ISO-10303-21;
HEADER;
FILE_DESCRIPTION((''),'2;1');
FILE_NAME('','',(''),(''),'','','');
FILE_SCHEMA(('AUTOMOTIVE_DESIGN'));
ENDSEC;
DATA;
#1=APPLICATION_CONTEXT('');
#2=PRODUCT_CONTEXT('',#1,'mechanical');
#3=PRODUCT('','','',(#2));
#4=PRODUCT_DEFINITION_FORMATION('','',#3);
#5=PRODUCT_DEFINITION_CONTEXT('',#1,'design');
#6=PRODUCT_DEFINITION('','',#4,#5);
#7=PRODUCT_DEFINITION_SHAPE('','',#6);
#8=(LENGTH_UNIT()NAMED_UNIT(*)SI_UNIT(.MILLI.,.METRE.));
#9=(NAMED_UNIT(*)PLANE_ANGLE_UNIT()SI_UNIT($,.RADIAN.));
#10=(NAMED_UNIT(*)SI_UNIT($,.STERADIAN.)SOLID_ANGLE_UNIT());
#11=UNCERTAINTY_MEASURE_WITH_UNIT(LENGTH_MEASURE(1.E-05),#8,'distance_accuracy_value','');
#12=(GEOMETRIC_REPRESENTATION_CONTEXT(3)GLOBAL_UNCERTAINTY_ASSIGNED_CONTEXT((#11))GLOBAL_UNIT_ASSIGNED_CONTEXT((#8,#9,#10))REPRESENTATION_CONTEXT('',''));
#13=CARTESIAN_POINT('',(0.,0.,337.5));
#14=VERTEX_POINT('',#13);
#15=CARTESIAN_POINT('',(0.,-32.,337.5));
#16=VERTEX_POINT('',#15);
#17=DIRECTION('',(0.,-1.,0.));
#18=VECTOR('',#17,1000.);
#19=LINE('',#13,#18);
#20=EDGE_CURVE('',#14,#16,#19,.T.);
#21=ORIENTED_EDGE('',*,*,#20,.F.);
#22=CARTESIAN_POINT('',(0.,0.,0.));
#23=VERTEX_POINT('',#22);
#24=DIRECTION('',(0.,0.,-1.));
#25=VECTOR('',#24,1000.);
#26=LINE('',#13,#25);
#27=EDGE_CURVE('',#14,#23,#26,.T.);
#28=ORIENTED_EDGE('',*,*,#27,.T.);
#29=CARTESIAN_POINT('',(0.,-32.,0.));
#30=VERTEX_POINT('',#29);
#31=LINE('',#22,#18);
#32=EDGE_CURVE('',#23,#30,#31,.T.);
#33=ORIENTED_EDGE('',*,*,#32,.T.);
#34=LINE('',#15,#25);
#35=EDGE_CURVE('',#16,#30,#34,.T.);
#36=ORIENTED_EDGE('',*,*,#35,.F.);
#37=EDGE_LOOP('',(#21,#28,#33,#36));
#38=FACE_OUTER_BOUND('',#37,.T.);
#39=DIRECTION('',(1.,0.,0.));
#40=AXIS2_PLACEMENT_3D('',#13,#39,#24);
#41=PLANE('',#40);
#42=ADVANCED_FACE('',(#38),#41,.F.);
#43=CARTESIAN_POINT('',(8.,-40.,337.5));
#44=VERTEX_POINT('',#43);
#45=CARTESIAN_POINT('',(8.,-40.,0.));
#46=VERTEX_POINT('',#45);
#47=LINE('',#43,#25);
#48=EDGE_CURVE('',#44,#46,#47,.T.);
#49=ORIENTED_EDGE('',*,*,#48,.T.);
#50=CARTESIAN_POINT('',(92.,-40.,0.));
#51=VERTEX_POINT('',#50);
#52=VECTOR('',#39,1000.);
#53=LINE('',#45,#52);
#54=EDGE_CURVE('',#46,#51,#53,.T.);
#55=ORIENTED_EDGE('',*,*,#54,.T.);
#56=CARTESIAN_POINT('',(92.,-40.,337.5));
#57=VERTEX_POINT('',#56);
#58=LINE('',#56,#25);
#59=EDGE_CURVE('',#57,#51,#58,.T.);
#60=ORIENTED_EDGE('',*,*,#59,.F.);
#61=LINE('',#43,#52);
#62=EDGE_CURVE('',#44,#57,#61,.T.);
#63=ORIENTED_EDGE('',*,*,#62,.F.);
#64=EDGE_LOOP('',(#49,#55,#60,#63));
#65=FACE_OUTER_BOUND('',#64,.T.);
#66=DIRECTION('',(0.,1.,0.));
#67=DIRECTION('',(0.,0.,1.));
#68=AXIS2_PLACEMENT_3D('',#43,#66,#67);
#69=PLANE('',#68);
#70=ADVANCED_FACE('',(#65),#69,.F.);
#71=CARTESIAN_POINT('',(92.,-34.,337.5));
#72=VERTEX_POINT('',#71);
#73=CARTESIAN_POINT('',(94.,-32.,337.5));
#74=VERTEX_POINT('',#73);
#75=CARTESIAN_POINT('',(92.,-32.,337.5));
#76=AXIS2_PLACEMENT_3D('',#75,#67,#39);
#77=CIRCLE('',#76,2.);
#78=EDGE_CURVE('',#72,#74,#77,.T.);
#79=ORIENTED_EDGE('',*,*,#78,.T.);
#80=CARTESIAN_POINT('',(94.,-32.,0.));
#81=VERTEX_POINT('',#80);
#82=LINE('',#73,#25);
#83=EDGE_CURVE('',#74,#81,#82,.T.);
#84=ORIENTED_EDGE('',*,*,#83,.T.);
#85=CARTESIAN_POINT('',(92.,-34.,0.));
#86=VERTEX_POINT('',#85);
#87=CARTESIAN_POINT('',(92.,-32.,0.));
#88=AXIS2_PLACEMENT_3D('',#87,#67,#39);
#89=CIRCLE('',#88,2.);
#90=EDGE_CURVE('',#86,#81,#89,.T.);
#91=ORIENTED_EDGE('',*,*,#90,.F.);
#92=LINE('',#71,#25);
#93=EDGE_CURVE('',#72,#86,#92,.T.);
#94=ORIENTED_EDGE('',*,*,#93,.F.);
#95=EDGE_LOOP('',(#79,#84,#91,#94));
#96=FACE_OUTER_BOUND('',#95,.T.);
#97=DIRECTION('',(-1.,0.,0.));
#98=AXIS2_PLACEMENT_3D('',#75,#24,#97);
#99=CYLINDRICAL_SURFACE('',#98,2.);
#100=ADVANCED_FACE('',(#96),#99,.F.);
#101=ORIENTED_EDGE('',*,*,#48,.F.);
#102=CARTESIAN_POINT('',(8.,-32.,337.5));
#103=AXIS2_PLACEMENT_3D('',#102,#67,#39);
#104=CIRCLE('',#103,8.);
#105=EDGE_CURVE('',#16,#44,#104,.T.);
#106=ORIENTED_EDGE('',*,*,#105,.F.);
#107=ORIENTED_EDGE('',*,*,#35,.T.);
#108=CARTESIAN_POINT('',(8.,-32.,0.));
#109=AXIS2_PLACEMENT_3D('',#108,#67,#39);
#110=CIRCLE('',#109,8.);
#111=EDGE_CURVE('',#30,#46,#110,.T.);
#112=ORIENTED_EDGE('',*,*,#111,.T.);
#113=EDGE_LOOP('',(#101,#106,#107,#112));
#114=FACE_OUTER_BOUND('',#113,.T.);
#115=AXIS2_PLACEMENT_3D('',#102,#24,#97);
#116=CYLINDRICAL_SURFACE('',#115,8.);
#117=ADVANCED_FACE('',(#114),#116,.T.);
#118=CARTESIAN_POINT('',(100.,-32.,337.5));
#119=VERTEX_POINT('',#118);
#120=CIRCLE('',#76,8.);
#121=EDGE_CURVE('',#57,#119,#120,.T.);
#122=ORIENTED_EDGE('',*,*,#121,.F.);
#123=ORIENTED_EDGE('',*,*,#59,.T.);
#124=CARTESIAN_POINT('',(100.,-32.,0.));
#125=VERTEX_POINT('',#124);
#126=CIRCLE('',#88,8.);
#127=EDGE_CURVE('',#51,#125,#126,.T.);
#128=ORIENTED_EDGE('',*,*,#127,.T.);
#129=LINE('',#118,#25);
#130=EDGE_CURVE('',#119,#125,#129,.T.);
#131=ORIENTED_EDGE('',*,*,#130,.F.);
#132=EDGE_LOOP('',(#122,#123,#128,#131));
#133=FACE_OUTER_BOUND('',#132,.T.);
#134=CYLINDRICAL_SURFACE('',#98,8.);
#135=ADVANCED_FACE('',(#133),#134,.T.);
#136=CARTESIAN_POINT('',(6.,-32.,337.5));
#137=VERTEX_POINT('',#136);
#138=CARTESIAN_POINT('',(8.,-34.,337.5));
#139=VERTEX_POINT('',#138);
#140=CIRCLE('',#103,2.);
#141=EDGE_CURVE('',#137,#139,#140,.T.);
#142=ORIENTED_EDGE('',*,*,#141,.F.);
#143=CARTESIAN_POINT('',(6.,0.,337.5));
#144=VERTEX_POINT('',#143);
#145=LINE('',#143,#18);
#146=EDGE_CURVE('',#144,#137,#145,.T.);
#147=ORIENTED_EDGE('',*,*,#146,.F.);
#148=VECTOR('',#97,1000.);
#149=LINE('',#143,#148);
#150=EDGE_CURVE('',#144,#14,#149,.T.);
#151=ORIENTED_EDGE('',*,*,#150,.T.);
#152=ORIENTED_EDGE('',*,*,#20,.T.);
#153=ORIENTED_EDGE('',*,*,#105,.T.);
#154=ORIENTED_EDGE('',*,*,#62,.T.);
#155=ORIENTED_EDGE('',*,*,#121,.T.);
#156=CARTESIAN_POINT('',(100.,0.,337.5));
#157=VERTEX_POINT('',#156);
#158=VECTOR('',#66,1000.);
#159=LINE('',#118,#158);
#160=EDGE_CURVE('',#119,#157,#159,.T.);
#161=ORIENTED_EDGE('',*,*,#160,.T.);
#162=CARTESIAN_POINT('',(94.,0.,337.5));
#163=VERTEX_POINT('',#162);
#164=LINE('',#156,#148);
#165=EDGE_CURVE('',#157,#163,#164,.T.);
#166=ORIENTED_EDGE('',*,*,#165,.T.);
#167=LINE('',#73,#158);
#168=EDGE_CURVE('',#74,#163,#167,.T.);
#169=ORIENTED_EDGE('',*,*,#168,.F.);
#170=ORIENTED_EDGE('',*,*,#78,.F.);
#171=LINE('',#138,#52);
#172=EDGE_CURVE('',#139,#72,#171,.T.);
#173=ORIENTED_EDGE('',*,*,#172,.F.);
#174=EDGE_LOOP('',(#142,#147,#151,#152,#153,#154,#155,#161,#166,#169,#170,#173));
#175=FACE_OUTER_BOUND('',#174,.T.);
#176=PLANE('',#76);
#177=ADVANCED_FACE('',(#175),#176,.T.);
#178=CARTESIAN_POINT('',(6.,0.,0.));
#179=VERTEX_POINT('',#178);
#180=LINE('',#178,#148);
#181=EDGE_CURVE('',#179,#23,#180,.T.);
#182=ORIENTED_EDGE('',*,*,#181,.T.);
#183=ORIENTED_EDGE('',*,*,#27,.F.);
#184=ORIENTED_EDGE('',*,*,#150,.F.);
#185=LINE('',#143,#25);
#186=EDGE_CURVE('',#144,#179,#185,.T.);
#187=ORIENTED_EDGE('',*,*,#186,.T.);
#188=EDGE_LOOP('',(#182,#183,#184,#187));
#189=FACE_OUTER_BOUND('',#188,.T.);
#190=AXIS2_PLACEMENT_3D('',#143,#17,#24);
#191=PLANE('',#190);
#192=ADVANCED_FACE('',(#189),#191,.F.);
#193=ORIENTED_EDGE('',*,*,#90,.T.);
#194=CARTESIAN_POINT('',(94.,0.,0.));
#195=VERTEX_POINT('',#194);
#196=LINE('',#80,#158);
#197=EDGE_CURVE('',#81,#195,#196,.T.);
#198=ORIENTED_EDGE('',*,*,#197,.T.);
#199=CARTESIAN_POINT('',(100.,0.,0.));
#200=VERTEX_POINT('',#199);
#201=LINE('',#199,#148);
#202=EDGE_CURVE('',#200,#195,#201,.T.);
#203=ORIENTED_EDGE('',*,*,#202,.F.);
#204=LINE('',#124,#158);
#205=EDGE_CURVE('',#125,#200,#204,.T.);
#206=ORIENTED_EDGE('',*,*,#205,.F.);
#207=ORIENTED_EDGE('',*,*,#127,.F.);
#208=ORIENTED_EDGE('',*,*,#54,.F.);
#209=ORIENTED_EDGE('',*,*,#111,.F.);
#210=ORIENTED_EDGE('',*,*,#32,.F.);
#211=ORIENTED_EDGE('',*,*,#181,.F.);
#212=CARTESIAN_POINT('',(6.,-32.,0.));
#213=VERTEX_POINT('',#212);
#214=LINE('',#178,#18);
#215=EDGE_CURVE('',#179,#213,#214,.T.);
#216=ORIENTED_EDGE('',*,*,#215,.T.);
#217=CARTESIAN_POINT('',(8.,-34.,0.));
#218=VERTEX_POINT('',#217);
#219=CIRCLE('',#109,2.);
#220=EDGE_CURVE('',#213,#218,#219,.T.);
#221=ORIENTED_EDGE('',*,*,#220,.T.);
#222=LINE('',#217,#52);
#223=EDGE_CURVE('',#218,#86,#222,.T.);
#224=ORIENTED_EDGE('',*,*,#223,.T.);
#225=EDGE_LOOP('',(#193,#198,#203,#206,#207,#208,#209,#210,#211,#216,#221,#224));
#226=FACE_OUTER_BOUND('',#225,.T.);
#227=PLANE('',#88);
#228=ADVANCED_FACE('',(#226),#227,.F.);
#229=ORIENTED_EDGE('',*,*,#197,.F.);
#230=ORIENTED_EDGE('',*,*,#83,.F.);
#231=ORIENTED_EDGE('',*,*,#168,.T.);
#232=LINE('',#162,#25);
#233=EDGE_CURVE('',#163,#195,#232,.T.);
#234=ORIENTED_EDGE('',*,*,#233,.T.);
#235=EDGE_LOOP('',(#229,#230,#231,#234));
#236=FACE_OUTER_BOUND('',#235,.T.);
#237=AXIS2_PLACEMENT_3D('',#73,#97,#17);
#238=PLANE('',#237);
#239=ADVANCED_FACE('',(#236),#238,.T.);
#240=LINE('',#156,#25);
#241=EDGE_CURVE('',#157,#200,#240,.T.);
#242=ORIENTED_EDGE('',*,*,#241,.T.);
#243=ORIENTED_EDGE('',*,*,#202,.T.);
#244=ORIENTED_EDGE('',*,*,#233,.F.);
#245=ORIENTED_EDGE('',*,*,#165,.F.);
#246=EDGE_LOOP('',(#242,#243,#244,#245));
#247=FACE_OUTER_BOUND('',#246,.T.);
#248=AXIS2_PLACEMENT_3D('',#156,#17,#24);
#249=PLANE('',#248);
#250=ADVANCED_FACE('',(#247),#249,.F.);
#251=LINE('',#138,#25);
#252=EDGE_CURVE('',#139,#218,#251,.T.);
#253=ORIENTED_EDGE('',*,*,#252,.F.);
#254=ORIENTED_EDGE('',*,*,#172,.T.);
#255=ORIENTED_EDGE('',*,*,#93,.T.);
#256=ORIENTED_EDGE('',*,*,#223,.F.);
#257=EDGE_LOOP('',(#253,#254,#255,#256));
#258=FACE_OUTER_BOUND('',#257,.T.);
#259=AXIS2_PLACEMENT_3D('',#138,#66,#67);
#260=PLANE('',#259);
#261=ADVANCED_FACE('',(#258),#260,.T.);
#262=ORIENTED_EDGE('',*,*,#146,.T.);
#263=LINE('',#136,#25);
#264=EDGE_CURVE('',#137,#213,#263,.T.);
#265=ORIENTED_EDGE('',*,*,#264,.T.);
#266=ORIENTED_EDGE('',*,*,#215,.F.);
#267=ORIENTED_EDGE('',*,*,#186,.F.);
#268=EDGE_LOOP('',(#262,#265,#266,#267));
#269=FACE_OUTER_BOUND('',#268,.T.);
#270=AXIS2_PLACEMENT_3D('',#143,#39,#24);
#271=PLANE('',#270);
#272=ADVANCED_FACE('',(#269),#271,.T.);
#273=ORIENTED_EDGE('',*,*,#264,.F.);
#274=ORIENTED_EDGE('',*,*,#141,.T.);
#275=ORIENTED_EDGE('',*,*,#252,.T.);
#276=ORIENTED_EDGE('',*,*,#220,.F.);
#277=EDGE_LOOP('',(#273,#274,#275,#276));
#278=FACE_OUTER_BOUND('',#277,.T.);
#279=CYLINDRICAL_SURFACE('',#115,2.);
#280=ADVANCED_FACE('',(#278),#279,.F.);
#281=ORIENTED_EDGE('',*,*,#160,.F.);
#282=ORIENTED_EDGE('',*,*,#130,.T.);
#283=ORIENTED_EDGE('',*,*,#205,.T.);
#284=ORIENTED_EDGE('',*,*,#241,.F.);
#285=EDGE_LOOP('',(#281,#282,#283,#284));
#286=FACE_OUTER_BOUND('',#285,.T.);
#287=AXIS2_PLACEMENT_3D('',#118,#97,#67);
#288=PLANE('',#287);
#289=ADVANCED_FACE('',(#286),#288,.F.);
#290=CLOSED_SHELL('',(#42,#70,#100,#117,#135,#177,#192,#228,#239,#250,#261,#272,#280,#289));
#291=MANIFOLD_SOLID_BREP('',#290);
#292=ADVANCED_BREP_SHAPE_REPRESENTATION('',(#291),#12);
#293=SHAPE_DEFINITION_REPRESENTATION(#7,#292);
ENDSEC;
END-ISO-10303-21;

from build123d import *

# Parameters (mm, degrees)
BOSS_EXTRUDE2_DEPTH = 337.5


with BuildPart() as part:
    # Sketch2 → Boss-Extrude2 (new body)
    with BuildSketch(Plane.XY):
        with BuildLine():
            Line((0, 0), (0, -32))
            ThreePointArc((0, -32), (2.343145751, -37.656854249), (8, -40))
            Line((8, -40), (92, -40))
            ThreePointArc((92, -40), (97.656854249, -37.656854249), (100, -32))
            Line((100, -32), (100, 0))
            Line((100, 0), (94, 0))
            Line((94, 0), (94, -32))
            ThreePointArc((94, -32), (93.414213562, -33.414213562), (92, -34))
            Line((92, -34), (8, -34))
            ThreePointArc((8, -34), (6.585786438, -33.414213562), (6, -32))
            Line((6, -32), (6, 0))
            Line((6, 0), (0, 0))
        make_face()
    extrude(amount=BOSS_EXTRUDE2_DEPTH)


solid = part.part
